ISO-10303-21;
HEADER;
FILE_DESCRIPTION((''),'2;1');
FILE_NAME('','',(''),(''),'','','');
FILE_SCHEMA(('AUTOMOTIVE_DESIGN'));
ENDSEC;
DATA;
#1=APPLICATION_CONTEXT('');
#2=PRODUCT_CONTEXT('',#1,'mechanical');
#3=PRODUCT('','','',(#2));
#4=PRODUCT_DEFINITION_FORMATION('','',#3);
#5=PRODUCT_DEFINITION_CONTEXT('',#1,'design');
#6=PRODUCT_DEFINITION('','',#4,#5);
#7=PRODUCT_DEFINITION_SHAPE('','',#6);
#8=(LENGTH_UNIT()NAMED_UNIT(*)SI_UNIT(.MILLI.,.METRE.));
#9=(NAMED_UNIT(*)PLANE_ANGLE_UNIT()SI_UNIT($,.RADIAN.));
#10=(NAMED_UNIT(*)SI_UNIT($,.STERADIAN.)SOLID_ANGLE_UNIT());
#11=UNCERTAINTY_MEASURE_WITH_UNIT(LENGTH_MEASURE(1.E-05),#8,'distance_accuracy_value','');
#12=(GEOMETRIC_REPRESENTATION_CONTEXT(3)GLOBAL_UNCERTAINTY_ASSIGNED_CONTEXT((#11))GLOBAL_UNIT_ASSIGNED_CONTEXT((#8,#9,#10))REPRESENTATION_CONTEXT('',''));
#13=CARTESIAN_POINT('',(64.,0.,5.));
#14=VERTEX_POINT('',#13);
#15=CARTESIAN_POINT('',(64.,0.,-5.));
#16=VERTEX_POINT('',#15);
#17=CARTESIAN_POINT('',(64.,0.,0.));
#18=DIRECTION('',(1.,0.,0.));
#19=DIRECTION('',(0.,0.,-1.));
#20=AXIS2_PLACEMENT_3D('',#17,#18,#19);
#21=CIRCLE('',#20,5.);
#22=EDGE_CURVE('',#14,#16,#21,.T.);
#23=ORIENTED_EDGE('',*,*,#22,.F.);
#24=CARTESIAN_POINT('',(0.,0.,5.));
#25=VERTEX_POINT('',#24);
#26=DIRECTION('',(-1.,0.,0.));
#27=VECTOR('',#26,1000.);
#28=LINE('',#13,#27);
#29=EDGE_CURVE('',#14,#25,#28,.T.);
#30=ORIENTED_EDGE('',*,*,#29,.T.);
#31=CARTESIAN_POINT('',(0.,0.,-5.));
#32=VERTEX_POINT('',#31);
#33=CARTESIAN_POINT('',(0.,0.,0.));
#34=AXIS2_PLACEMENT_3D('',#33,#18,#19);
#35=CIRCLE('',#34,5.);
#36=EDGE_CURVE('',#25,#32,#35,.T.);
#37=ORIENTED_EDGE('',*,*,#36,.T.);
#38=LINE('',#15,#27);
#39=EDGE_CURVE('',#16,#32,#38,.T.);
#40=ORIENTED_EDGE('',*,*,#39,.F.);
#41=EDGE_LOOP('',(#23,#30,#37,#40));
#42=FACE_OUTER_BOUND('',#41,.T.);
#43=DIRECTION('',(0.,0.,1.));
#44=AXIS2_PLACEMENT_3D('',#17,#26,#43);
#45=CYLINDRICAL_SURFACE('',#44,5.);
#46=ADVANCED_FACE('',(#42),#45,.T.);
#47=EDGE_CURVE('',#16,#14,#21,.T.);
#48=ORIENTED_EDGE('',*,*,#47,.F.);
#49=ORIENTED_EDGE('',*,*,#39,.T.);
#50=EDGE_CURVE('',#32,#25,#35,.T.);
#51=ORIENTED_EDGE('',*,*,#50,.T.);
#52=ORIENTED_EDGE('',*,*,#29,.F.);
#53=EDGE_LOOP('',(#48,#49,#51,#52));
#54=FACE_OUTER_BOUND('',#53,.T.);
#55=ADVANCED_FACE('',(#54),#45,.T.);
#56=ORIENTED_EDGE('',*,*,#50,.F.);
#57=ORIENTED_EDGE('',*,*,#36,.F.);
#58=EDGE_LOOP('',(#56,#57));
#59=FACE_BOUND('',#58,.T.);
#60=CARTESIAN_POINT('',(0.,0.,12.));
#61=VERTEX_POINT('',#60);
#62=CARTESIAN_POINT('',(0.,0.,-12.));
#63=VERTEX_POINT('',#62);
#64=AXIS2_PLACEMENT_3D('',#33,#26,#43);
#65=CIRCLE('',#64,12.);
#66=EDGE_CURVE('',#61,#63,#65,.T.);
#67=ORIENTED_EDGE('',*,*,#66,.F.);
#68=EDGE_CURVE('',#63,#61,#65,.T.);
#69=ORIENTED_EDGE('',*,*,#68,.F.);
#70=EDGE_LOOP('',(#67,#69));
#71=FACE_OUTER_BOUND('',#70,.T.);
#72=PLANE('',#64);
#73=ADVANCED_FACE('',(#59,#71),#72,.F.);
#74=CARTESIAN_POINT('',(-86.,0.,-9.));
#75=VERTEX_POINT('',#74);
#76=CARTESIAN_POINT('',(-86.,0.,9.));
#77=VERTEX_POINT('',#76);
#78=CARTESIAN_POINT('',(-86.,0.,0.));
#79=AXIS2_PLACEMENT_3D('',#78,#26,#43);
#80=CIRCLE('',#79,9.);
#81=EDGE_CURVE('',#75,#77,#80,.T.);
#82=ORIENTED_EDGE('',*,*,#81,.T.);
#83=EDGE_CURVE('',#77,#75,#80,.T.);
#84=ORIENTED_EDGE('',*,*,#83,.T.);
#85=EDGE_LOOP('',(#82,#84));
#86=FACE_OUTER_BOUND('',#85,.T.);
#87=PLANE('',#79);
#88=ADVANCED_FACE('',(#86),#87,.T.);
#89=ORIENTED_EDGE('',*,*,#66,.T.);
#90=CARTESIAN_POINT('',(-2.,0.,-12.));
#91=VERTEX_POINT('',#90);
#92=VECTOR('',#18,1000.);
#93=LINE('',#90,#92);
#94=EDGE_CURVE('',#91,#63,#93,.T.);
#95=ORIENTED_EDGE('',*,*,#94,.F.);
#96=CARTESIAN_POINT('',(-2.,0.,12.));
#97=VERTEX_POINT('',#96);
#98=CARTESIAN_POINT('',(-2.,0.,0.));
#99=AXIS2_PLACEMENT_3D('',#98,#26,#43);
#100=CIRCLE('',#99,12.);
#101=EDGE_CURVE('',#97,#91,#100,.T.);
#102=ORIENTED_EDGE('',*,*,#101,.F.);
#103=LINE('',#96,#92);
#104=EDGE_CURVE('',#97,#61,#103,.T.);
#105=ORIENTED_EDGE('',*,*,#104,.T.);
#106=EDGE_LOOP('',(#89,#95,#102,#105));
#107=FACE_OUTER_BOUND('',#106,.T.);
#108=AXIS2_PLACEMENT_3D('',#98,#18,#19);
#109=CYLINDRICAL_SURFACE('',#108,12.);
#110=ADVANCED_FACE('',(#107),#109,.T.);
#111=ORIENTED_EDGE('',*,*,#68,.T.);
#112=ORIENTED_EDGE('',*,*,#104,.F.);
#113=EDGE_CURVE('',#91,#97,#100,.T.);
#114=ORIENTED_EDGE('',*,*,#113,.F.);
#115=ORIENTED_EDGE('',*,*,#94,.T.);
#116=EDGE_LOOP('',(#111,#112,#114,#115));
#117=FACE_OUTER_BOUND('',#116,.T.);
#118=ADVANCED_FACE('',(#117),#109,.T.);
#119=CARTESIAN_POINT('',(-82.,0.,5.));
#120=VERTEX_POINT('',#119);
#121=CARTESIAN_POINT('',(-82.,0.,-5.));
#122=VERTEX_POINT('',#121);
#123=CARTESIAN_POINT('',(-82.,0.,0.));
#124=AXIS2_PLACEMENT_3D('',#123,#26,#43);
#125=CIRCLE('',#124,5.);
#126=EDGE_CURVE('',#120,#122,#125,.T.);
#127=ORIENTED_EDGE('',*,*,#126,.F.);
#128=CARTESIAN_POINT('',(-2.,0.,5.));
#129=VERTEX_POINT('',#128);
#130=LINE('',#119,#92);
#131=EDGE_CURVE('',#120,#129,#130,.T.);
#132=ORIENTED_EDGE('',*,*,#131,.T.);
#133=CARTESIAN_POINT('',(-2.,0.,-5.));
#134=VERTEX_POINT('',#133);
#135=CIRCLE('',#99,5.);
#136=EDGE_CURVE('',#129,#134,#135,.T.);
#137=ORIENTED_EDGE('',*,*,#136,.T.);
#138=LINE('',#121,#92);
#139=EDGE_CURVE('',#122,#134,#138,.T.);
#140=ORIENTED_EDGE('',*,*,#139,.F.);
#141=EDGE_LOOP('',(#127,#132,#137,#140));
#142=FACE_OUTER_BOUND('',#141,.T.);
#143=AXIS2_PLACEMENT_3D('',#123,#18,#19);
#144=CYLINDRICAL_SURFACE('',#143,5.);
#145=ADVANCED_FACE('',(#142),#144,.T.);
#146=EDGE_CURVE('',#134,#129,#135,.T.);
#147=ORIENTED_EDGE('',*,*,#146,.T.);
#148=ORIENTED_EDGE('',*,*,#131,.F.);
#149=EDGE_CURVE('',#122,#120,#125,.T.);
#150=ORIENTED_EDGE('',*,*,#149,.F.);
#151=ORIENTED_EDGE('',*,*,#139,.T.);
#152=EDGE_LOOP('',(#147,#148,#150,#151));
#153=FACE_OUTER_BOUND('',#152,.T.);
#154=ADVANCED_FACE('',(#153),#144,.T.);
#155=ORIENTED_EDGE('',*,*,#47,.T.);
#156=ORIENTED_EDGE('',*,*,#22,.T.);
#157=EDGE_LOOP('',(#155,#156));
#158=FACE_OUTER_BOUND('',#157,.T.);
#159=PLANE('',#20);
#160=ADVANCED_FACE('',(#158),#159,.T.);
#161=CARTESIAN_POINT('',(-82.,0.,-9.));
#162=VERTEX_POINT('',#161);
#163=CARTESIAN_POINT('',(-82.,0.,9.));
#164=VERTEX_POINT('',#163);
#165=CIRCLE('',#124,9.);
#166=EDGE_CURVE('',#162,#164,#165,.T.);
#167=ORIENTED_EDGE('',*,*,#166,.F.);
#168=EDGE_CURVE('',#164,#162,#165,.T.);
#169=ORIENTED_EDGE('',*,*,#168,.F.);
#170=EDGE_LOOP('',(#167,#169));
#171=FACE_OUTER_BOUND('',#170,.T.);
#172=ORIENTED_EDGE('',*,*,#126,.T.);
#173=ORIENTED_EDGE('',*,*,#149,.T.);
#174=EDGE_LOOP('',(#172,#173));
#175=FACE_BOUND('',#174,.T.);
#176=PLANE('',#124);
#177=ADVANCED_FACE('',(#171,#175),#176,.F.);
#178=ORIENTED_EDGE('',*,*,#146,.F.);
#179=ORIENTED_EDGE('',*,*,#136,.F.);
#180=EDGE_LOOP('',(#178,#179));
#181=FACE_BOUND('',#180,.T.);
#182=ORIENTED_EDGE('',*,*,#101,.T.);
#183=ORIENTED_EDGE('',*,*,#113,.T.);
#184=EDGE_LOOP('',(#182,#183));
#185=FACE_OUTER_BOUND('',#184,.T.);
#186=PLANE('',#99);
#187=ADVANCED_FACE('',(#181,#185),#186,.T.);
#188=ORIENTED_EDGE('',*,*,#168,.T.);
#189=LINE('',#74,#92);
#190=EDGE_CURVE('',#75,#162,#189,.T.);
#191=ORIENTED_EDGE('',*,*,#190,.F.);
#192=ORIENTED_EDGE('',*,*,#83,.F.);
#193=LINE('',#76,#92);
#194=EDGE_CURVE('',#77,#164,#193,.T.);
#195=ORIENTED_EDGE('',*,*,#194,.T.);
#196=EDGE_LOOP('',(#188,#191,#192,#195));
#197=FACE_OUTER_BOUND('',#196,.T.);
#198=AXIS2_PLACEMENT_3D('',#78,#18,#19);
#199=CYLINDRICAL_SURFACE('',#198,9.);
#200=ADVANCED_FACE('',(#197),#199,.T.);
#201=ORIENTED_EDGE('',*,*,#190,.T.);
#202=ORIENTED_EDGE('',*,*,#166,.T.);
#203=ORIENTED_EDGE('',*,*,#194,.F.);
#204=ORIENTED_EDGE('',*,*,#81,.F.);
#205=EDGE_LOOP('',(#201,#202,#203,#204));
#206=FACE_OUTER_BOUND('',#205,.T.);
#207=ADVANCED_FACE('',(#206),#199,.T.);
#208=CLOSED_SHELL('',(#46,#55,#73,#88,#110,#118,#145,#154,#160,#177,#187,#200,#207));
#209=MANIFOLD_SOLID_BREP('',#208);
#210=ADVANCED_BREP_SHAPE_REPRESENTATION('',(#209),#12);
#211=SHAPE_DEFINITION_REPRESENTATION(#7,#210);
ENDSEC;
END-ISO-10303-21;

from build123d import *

# Parameters (mm, degrees)
SHAFT_SECTION_A_PROFILE_10_R = 5
SHAFT_SECTION_A_10X64_DEPTH  = 64
COLLAR_PROFILE_24_R          = 12
COLLAR_24X2_DEPTH            = 2
SHAFT_START                  = 80
SHAFT_SECTION_B_PROFILE_10_R = 5
SHAFT_SECTION_B_10X80_DEPTH  = 80
HEAD_PROFILE_18_R            = 9
HEAD_18X4_DEPTH              = 4


with BuildPart() as part:
    # Shaft Section A Profile Ø10 → Shaft Section A Ø10x64 (new body)
    with BuildSketch(Plane(origin=(0, 0, 0), x_dir=(0, 0, -1), z_dir=(1, 0, 0))):
        Circle(SHAFT_SECTION_A_PROFILE_10_R)
    extrude(amount=SHAFT_SECTION_A_10X64_DEPTH)

    # Collar Profile Ø24 → Collar Ø24x2 (add)
    with BuildSketch(Plane.ZY):
        Circle(COLLAR_PROFILE_24_R)
    extrude(amount=COLLAR_24X2_DEPTH)

    # Shaft Section B Profile Ø10 → Shaft Section B Ø10x80 (add)
    with BuildSketch(Plane.ZY.offset(2).offset(SHAFT_START)):
        with Locations(Location((0, 0, 0), (0, 0, 180))):
            Circle(SHAFT_SECTION_B_PROFILE_10_R)
    extrude(amount=-SHAFT_SECTION_B_10X80_DEPTH)

    # Head Profile Ø18 → Head Ø18x4 (add)
    with BuildSketch(Plane.ZY.offset(82)):
        Circle(HEAD_PROFILE_18_R)
    extrude(amount=HEAD_18X4_DEPTH)


solid = part.part
